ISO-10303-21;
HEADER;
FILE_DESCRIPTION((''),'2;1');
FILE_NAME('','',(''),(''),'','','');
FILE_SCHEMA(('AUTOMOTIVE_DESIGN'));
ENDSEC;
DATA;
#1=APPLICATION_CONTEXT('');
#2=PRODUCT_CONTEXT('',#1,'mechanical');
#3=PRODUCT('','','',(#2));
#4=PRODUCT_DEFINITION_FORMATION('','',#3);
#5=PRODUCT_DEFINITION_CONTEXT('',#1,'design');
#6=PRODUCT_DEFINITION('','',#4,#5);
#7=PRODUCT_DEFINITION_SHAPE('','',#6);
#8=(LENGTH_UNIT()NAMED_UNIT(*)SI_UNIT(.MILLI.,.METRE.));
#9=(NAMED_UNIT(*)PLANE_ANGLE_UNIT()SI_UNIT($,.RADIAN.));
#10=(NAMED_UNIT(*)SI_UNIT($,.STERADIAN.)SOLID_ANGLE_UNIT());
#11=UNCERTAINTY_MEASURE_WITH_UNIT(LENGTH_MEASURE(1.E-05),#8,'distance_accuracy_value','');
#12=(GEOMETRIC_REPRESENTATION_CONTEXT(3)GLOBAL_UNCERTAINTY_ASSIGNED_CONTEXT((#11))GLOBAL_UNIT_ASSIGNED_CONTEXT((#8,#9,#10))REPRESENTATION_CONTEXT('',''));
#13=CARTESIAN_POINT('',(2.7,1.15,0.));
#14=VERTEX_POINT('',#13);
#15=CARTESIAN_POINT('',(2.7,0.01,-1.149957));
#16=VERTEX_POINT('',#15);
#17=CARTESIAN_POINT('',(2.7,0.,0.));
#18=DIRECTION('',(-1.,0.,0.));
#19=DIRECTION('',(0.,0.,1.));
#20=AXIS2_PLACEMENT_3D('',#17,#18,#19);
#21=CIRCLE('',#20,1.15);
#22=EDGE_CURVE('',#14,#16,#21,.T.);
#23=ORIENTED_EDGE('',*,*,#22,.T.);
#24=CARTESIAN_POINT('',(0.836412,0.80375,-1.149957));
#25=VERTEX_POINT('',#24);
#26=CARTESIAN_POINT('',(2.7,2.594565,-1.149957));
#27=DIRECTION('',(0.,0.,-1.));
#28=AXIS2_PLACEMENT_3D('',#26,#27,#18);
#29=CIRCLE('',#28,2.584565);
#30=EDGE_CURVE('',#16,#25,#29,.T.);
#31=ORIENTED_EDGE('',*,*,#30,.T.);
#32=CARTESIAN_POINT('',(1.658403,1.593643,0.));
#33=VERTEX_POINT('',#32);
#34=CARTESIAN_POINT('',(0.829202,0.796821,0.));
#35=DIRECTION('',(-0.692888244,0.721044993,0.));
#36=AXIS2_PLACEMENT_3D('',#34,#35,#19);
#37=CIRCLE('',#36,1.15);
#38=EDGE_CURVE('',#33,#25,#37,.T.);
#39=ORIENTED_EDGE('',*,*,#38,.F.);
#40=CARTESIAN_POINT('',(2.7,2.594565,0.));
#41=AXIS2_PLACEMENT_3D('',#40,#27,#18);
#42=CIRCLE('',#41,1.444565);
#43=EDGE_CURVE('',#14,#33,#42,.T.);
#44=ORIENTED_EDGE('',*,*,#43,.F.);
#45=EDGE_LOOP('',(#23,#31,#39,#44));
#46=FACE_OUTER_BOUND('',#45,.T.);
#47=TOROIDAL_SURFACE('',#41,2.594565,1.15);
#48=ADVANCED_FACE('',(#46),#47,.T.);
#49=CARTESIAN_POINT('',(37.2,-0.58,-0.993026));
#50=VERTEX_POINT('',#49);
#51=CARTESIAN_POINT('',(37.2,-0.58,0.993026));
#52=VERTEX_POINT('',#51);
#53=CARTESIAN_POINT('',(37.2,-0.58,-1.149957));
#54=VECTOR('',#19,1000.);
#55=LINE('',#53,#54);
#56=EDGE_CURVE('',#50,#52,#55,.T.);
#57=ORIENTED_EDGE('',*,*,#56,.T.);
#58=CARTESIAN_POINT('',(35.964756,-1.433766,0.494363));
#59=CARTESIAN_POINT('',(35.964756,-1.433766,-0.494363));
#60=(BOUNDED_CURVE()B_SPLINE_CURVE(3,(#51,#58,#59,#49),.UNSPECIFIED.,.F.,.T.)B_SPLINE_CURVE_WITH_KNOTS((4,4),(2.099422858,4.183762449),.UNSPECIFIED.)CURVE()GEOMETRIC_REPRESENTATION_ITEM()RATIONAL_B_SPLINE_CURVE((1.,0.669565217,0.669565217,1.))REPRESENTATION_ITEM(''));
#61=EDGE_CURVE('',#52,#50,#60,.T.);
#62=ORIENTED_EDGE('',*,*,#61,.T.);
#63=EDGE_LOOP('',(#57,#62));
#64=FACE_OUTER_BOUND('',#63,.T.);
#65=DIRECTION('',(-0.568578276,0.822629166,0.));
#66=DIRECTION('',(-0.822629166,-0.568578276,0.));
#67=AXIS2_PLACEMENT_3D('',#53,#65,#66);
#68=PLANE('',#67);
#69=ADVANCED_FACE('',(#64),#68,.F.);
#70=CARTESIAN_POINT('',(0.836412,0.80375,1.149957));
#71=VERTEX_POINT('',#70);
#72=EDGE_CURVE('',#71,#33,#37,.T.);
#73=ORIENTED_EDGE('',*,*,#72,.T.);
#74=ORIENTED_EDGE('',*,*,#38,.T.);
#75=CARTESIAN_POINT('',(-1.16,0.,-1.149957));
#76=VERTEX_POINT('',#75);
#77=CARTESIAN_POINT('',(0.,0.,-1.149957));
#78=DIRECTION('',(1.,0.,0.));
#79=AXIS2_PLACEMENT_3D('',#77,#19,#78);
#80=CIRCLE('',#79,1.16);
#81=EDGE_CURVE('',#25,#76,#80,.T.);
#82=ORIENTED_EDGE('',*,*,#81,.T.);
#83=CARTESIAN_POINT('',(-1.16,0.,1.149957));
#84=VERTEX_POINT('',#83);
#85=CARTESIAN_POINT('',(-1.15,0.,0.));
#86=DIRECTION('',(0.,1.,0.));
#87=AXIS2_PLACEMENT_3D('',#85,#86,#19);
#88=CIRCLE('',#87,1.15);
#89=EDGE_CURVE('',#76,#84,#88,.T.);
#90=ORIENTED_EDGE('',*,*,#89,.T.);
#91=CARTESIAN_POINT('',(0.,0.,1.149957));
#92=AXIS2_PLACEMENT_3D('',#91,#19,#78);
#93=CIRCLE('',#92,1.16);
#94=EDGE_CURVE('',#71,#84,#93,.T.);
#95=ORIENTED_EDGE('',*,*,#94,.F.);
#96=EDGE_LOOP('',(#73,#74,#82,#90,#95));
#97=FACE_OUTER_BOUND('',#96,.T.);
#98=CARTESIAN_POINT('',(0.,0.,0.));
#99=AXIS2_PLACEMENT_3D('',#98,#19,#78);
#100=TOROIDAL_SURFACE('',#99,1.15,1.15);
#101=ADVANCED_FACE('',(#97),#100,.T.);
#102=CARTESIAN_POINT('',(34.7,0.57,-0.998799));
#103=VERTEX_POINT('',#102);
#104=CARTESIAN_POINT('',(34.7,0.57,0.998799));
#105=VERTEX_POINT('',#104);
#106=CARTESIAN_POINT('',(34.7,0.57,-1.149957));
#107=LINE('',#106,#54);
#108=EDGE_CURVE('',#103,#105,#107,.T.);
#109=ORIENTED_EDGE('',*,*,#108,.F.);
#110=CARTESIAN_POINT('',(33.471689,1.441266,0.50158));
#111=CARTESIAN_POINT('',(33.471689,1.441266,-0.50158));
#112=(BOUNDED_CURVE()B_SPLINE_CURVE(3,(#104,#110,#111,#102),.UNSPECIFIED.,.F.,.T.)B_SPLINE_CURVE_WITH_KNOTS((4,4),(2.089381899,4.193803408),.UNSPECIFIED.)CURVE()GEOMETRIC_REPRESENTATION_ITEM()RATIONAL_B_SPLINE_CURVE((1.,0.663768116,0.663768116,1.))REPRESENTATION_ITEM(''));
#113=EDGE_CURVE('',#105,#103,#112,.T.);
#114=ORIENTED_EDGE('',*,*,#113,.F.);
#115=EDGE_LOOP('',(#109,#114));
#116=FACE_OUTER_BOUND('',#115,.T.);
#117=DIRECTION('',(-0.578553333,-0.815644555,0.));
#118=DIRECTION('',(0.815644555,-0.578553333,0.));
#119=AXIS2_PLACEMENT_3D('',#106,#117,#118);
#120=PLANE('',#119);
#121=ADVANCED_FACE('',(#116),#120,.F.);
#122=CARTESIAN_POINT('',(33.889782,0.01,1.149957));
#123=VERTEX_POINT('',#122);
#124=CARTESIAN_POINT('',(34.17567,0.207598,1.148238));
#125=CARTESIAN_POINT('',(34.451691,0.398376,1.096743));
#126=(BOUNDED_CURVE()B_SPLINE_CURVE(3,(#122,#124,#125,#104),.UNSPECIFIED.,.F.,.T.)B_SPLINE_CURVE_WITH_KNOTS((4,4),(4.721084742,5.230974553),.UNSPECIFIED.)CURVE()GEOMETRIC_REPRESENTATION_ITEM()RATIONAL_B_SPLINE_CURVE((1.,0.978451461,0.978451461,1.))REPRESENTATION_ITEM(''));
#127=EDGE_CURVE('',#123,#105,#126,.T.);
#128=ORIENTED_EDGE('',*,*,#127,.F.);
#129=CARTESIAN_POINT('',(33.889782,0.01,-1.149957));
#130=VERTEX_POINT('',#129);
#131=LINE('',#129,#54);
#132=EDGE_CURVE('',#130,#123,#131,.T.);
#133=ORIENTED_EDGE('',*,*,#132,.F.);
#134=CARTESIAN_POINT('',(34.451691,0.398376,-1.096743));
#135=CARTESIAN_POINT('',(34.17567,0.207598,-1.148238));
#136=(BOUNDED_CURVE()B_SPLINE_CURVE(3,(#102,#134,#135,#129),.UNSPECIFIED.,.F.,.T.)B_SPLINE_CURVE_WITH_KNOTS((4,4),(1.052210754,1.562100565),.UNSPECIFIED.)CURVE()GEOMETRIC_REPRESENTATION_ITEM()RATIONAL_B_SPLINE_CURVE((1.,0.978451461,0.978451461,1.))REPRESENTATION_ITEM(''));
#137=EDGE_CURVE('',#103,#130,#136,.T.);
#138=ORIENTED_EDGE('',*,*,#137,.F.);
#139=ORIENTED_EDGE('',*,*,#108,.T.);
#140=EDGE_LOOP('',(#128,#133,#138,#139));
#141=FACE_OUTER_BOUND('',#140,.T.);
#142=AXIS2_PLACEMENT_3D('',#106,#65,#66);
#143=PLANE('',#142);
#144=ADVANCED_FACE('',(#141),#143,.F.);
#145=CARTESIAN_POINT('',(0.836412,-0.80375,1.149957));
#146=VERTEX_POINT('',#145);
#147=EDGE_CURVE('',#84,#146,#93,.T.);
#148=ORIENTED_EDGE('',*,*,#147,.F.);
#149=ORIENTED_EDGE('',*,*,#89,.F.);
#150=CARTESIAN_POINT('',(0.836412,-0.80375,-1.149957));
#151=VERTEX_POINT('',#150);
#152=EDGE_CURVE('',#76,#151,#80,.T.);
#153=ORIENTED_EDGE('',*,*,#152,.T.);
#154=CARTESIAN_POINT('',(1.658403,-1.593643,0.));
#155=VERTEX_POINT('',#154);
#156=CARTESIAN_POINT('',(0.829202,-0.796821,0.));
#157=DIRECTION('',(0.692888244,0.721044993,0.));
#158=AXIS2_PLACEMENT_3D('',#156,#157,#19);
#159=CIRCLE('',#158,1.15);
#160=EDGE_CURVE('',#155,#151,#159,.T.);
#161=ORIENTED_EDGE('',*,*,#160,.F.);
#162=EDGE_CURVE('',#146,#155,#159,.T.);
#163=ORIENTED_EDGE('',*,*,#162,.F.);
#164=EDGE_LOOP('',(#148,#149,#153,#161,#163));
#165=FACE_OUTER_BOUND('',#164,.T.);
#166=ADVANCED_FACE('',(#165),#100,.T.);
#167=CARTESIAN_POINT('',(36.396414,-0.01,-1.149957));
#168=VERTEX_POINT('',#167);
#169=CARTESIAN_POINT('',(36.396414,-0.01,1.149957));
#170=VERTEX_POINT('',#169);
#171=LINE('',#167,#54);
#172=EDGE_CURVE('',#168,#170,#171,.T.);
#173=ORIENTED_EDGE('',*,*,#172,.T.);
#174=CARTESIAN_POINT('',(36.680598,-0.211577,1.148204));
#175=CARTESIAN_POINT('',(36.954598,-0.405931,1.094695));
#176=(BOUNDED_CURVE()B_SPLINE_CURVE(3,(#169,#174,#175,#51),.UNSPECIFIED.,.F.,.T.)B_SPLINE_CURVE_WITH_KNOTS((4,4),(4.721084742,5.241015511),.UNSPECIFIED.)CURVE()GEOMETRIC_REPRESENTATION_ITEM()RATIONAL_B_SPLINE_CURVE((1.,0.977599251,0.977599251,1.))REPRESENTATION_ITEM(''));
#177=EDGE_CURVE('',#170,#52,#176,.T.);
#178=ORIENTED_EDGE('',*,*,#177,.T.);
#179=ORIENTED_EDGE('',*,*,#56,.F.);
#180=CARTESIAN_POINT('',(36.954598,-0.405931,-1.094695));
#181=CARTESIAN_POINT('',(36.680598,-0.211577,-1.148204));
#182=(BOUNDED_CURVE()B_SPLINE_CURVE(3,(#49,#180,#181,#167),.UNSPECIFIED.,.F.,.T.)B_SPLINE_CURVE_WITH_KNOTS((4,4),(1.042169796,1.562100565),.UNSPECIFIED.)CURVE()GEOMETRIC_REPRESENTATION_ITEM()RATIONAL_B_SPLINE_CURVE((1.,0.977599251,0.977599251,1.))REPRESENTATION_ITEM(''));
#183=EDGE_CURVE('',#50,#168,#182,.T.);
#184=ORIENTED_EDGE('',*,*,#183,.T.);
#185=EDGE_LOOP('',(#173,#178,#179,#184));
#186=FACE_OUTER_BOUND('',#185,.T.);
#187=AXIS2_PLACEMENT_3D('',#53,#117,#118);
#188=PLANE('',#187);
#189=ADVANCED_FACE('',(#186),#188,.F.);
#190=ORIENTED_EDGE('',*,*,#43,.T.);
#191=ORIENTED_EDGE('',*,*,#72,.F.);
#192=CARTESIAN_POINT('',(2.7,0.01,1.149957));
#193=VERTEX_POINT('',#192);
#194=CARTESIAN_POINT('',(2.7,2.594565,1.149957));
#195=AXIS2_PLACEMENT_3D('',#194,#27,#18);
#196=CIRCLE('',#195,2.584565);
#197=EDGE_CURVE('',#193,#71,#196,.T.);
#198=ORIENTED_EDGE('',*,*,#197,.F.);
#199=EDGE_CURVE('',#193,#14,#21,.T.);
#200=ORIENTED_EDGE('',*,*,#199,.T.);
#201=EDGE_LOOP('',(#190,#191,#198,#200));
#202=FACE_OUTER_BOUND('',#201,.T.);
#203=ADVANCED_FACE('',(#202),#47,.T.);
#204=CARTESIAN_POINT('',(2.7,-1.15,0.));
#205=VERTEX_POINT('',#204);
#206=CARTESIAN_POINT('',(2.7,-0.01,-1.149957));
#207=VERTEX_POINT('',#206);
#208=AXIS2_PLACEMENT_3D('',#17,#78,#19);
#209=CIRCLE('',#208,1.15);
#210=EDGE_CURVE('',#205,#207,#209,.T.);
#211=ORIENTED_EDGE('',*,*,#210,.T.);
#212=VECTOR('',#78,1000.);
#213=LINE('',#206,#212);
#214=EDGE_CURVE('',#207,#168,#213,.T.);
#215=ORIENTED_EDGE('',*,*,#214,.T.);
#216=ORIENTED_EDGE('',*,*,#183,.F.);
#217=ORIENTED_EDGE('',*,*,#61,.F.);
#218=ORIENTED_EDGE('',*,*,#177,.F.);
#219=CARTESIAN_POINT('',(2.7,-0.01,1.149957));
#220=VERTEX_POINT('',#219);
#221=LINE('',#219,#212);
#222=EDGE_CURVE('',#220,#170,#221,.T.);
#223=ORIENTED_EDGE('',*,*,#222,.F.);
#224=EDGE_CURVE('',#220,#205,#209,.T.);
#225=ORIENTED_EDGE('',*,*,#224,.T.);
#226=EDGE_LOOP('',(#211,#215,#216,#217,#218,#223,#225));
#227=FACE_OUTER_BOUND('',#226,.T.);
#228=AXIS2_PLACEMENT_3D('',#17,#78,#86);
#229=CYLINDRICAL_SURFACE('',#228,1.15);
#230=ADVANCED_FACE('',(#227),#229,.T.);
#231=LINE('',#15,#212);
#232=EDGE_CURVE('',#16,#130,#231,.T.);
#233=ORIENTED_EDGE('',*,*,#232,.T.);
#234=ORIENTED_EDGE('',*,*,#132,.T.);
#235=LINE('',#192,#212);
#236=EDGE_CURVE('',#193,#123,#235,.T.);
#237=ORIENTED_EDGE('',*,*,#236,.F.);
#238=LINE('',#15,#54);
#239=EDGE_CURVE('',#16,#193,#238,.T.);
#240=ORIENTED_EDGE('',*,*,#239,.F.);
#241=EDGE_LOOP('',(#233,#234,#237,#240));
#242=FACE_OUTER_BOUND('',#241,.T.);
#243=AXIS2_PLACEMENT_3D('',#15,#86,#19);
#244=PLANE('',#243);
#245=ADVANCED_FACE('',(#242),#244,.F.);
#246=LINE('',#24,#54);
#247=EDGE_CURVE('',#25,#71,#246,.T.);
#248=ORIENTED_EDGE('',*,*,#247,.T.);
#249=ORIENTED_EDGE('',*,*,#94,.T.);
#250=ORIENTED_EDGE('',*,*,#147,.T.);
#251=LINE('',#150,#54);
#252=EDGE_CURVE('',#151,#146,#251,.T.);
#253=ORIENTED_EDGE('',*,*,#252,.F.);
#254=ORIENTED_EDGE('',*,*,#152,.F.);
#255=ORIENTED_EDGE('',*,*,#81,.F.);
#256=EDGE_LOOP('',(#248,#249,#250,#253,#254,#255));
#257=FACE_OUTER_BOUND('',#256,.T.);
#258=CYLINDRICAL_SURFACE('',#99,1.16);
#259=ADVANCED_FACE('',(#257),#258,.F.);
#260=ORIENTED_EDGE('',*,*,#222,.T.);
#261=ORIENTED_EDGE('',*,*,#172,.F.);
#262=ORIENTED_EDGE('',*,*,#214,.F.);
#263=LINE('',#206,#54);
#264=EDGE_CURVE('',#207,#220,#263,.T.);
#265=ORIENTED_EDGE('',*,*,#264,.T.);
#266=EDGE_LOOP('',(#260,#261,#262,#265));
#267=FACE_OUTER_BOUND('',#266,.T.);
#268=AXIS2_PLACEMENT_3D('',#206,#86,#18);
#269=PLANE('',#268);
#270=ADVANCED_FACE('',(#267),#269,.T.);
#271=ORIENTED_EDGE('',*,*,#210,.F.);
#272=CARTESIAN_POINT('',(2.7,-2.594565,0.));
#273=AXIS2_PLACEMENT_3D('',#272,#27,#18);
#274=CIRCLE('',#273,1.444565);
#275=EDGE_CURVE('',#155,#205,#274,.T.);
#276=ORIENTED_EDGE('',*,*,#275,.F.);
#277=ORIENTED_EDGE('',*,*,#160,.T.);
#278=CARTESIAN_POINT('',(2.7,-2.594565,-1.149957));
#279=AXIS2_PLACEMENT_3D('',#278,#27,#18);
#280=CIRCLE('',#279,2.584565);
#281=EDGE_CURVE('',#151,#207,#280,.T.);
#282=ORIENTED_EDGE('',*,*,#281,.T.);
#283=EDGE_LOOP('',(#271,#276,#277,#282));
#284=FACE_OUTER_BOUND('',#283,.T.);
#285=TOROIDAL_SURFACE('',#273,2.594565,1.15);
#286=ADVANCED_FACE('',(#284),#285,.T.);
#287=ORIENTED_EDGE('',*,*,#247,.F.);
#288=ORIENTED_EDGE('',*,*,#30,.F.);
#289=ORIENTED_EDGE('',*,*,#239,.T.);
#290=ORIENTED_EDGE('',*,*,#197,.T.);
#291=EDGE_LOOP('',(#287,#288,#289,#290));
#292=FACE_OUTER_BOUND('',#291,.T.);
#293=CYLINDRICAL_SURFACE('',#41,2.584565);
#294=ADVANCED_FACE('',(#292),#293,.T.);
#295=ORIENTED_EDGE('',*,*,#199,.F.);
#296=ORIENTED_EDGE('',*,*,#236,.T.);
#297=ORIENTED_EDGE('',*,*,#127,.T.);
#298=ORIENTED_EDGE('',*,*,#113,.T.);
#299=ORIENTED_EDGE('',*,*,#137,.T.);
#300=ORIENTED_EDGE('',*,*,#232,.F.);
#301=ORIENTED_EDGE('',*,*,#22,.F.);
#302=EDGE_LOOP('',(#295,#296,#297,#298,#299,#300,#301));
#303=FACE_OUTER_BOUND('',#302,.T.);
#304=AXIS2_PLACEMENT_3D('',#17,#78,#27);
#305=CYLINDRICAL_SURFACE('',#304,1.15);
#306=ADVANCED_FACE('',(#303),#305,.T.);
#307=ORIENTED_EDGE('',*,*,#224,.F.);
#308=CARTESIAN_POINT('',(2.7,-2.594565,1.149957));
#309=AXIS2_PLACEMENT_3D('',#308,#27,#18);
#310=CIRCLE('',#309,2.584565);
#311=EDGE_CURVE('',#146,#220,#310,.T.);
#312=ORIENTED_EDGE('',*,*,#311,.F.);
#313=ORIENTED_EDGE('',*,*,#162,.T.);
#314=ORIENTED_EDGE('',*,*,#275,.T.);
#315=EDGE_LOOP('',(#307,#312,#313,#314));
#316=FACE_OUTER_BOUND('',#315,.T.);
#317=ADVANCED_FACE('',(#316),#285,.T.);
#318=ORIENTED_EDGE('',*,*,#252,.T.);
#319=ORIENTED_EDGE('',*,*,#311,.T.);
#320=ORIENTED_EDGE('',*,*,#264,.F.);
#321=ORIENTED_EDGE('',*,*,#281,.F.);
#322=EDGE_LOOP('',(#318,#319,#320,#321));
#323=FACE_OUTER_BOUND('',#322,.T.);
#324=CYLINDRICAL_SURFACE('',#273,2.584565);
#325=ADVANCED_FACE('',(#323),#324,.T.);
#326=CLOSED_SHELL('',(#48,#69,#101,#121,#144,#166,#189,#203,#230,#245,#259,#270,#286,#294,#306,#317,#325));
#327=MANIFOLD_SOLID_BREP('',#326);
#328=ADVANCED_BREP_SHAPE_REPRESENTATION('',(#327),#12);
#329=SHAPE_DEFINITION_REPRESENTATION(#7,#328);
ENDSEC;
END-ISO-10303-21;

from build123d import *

# Parameters (mm, degrees)
CUT_EXTRUDE1_DEPTH      = 38.288770437
CUT_EXTRUDE1_DEPTH_BACK = 38.288770437


with BuildPart() as part:
    # Sweep2: sweep along a path in Dimension Sketch
    with BuildLine(Plane.XY) as sweep2_path:
        Line((34.7, 1.15), (2.7, 1.15))
        ThreePointArc((2.7, 1.15), (2.133929691, 1.265530578), (1.658403483, 1.593642961))
        ThreePointArc((1.658403483, 1.593642961), (-2.3, 0), (1.658403483, -1.593642961))
        ThreePointArc((1.658403483, -1.593642961), (2.133929691, -1.265530578), (2.7, -1.15))
        Line((2.7, -1.15), (37.2, -1.15))
    # Sketch2 → Sweep2 (sweep)
    with BuildSketch(Plane(origin=(34.7, 1.15, 0), x_dir=(0, 0, 1), z_dir=(-1, 0, 0))):
        with BuildLine():
            Line((-1.149956521, -1.14), (1.149956521, -1.14))
            ThreePointArc((1.149956521, -1.14), (0, 0), (-1.149956521, -1.14))
        make_face()
    sweep(path=sweep2_path.line)

    # Sketch3 → Cut-Extrude1 (cut, two sides: drawn at the far end of the back side and taken through both)
    with BuildSketch(Plane.XY.offset(-CUT_EXTRUDE1_DEPTH_BACK)):
        Polygon((34.7, 0.57), (33.882315934, 1.15), (37.21, 1.15), (37.21, -1.15), (36.375313858, -1.15), (37.2, -0.58), (36.382315934, 0), (33.875313858, 0), align=None)
    extrude(amount=CUT_EXTRUDE1_DEPTH + CUT_EXTRUDE1_DEPTH_BACK, mode=Mode.SUBTRACT)


solid = part.part
